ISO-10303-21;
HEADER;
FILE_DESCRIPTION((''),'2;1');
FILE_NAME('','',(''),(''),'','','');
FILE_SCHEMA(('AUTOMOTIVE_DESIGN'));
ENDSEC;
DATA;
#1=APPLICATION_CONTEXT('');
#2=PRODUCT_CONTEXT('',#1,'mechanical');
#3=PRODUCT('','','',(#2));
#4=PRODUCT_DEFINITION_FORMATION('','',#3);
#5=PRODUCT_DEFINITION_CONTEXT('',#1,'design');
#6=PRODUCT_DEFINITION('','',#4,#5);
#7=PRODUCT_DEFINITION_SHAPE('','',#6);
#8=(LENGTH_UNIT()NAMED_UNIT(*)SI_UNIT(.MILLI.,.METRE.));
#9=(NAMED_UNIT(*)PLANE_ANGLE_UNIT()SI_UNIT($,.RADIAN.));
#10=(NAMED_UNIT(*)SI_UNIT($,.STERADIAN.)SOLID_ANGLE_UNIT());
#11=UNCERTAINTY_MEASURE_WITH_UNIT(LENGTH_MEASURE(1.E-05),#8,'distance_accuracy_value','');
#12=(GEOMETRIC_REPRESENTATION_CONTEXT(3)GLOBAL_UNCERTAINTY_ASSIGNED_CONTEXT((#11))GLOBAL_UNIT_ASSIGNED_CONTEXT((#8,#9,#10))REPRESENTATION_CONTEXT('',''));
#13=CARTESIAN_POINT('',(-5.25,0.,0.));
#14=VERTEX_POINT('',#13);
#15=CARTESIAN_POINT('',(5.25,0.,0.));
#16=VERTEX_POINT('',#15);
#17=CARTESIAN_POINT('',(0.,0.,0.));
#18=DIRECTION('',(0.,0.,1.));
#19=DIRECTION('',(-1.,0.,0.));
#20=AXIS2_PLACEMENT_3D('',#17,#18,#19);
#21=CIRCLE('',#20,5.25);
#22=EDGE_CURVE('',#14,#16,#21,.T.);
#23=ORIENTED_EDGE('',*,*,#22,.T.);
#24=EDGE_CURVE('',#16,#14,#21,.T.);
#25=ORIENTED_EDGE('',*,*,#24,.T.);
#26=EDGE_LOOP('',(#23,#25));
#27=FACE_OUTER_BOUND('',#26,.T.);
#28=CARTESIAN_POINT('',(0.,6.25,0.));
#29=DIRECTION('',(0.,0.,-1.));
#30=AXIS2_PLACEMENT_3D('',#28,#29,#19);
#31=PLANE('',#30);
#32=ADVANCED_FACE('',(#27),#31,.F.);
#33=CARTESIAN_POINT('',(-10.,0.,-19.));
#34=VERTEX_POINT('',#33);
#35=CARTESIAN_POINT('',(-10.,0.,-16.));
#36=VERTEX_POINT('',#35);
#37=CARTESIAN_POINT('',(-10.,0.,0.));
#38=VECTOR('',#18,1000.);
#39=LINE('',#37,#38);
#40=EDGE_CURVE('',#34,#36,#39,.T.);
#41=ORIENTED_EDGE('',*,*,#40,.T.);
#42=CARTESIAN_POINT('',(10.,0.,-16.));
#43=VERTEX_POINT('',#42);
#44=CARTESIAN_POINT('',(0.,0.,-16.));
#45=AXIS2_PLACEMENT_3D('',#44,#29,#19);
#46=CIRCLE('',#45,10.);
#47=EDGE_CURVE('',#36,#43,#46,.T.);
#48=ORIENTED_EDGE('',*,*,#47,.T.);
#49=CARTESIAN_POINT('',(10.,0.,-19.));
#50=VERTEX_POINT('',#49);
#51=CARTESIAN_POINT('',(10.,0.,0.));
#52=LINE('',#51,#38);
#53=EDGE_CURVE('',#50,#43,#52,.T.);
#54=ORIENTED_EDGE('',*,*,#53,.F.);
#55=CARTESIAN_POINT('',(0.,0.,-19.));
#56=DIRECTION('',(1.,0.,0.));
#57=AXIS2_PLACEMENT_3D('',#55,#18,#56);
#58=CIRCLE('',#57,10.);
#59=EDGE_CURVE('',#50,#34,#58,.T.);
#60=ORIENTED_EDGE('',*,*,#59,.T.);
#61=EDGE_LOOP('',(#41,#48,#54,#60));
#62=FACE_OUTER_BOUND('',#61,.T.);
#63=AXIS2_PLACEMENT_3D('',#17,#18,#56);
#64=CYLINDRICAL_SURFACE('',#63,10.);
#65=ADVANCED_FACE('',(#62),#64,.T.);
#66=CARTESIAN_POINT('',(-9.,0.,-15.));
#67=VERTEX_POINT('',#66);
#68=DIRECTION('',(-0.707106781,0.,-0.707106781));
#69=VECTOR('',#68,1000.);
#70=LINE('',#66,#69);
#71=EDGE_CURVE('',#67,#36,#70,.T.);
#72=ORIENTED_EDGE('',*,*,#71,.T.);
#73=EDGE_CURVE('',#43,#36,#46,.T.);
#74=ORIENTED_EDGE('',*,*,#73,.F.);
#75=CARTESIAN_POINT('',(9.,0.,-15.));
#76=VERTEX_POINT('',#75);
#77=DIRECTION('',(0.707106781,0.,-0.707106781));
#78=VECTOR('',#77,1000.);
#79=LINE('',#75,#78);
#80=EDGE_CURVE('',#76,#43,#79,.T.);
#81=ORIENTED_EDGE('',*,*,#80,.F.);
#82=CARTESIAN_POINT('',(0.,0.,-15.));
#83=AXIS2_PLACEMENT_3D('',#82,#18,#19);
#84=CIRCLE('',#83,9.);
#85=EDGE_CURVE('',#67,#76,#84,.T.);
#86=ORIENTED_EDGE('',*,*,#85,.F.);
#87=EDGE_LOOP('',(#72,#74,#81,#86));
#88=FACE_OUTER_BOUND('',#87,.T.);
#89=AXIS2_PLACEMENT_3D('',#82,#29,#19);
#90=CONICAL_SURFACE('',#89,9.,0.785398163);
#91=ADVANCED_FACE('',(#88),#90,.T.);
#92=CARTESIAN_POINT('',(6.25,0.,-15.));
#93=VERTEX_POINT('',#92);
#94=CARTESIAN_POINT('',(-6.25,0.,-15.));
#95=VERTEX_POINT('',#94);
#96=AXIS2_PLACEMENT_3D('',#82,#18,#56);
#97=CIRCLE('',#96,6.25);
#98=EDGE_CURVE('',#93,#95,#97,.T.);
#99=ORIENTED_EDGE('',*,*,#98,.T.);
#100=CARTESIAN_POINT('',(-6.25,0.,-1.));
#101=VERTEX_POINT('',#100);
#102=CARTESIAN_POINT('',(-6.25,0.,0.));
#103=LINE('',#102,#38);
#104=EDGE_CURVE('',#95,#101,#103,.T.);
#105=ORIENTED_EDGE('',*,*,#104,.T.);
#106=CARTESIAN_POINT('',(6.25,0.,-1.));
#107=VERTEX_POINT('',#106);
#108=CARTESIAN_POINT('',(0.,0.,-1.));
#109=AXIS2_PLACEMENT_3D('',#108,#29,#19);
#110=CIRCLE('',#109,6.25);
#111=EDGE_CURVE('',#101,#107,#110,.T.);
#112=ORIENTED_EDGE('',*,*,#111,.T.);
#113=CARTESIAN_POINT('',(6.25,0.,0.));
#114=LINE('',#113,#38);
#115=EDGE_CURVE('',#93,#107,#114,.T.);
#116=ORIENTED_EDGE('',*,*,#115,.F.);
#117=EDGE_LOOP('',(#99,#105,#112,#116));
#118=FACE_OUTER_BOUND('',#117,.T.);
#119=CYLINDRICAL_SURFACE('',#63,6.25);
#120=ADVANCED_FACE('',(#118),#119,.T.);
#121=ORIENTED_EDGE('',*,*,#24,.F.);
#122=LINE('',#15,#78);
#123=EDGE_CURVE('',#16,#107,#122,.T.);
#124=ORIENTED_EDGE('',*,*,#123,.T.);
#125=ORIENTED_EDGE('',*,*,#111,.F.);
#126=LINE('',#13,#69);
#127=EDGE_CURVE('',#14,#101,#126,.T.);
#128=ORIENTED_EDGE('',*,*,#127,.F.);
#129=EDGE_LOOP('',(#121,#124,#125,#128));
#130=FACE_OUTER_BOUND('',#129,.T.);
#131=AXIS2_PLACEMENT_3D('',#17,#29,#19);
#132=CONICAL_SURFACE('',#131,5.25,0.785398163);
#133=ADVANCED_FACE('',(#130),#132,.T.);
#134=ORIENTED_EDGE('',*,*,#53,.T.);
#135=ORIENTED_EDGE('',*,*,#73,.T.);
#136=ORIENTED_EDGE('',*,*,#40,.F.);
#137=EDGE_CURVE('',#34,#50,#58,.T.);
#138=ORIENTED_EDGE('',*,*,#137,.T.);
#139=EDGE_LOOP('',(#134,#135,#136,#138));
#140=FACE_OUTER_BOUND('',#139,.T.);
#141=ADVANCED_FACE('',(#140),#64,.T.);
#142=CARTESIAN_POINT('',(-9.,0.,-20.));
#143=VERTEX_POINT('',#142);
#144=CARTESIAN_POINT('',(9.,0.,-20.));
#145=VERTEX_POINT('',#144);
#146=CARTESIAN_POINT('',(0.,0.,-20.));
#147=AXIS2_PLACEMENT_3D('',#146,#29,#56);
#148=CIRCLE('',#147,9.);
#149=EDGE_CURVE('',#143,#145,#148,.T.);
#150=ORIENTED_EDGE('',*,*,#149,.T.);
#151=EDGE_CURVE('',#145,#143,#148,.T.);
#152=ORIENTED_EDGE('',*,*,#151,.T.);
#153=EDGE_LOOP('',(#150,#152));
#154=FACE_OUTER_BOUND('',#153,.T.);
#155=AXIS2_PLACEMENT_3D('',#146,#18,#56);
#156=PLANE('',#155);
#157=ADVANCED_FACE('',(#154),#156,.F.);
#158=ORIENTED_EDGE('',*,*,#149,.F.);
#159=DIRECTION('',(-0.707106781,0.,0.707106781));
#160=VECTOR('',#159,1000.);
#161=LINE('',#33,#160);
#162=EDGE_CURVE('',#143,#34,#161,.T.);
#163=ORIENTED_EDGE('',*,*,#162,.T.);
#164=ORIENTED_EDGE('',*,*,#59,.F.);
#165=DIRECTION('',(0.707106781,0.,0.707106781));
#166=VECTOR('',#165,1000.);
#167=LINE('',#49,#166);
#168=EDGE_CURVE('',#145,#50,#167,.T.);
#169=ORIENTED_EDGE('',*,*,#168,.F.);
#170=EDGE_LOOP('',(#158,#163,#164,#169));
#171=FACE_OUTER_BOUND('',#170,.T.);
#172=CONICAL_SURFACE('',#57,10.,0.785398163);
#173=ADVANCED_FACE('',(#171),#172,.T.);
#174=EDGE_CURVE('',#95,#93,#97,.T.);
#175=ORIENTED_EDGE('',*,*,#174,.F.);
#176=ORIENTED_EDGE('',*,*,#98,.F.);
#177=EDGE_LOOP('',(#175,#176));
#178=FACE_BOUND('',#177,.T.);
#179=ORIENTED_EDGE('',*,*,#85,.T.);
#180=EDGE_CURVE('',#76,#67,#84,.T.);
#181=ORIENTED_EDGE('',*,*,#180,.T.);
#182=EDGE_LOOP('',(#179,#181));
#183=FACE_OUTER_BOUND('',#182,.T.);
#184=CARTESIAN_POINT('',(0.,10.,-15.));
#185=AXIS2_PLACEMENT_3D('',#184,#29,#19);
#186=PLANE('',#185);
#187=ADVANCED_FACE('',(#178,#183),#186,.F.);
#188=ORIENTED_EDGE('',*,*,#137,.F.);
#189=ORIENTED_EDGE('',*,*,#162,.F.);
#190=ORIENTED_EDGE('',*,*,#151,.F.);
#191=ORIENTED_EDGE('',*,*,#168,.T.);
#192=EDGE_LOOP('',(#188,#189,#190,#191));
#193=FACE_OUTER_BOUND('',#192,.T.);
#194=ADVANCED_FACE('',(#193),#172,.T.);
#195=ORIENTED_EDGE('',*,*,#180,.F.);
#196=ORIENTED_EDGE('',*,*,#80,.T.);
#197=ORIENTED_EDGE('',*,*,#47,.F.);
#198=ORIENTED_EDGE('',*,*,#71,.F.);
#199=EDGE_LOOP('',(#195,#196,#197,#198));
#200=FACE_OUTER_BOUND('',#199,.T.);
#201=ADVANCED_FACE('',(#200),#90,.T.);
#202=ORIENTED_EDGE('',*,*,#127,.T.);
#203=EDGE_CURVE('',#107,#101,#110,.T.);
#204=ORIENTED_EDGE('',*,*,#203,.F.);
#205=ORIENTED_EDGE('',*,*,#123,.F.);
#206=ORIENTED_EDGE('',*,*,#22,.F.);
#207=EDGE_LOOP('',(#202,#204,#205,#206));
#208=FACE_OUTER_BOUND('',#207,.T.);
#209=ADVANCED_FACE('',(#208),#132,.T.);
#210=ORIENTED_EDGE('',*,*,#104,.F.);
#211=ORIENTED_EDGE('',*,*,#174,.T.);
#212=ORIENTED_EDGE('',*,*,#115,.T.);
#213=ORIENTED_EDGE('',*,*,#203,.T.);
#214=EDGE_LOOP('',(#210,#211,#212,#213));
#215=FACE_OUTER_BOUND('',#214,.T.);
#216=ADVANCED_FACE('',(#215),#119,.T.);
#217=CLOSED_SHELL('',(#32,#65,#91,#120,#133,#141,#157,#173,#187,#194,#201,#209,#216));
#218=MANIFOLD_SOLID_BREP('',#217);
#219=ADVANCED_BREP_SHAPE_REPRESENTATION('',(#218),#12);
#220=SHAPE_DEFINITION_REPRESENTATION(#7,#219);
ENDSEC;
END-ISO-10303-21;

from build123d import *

# Parameters (mm, degrees)
CHAMFER1_SIZE = 1


with BuildPart() as part:
    # Sketch1 → Revolve1 (revolve)
    with BuildSketch(Plane(origin=(0, 0, 0), x_dir=(0, 0, -1), z_dir=(1, 0, 0)), mode=Mode.PRIVATE) as revolve1_sk:
        Polygon((20, 0), (20, 10), (15, 10), (15, 6.25), (0, 6.25), (0, 0), align=None)
    revolve(revolve1_sk.sketch.rotate(Axis((0, 0, 0), (0, 0, -1)), 90), axis=Axis((0, 0, 0), (0, 0, -1)))

    # Chamfer1
    chamfer1_edges = [part.edges().sort_by_distance(p)[0] for p in [
        (-6.25, 0, 0),
        (-10, 0, -15),
        (-10, 0, -20),
    ]]
    chamfer(chamfer1_edges, length=CHAMFER1_SIZE)


solid = part.part
